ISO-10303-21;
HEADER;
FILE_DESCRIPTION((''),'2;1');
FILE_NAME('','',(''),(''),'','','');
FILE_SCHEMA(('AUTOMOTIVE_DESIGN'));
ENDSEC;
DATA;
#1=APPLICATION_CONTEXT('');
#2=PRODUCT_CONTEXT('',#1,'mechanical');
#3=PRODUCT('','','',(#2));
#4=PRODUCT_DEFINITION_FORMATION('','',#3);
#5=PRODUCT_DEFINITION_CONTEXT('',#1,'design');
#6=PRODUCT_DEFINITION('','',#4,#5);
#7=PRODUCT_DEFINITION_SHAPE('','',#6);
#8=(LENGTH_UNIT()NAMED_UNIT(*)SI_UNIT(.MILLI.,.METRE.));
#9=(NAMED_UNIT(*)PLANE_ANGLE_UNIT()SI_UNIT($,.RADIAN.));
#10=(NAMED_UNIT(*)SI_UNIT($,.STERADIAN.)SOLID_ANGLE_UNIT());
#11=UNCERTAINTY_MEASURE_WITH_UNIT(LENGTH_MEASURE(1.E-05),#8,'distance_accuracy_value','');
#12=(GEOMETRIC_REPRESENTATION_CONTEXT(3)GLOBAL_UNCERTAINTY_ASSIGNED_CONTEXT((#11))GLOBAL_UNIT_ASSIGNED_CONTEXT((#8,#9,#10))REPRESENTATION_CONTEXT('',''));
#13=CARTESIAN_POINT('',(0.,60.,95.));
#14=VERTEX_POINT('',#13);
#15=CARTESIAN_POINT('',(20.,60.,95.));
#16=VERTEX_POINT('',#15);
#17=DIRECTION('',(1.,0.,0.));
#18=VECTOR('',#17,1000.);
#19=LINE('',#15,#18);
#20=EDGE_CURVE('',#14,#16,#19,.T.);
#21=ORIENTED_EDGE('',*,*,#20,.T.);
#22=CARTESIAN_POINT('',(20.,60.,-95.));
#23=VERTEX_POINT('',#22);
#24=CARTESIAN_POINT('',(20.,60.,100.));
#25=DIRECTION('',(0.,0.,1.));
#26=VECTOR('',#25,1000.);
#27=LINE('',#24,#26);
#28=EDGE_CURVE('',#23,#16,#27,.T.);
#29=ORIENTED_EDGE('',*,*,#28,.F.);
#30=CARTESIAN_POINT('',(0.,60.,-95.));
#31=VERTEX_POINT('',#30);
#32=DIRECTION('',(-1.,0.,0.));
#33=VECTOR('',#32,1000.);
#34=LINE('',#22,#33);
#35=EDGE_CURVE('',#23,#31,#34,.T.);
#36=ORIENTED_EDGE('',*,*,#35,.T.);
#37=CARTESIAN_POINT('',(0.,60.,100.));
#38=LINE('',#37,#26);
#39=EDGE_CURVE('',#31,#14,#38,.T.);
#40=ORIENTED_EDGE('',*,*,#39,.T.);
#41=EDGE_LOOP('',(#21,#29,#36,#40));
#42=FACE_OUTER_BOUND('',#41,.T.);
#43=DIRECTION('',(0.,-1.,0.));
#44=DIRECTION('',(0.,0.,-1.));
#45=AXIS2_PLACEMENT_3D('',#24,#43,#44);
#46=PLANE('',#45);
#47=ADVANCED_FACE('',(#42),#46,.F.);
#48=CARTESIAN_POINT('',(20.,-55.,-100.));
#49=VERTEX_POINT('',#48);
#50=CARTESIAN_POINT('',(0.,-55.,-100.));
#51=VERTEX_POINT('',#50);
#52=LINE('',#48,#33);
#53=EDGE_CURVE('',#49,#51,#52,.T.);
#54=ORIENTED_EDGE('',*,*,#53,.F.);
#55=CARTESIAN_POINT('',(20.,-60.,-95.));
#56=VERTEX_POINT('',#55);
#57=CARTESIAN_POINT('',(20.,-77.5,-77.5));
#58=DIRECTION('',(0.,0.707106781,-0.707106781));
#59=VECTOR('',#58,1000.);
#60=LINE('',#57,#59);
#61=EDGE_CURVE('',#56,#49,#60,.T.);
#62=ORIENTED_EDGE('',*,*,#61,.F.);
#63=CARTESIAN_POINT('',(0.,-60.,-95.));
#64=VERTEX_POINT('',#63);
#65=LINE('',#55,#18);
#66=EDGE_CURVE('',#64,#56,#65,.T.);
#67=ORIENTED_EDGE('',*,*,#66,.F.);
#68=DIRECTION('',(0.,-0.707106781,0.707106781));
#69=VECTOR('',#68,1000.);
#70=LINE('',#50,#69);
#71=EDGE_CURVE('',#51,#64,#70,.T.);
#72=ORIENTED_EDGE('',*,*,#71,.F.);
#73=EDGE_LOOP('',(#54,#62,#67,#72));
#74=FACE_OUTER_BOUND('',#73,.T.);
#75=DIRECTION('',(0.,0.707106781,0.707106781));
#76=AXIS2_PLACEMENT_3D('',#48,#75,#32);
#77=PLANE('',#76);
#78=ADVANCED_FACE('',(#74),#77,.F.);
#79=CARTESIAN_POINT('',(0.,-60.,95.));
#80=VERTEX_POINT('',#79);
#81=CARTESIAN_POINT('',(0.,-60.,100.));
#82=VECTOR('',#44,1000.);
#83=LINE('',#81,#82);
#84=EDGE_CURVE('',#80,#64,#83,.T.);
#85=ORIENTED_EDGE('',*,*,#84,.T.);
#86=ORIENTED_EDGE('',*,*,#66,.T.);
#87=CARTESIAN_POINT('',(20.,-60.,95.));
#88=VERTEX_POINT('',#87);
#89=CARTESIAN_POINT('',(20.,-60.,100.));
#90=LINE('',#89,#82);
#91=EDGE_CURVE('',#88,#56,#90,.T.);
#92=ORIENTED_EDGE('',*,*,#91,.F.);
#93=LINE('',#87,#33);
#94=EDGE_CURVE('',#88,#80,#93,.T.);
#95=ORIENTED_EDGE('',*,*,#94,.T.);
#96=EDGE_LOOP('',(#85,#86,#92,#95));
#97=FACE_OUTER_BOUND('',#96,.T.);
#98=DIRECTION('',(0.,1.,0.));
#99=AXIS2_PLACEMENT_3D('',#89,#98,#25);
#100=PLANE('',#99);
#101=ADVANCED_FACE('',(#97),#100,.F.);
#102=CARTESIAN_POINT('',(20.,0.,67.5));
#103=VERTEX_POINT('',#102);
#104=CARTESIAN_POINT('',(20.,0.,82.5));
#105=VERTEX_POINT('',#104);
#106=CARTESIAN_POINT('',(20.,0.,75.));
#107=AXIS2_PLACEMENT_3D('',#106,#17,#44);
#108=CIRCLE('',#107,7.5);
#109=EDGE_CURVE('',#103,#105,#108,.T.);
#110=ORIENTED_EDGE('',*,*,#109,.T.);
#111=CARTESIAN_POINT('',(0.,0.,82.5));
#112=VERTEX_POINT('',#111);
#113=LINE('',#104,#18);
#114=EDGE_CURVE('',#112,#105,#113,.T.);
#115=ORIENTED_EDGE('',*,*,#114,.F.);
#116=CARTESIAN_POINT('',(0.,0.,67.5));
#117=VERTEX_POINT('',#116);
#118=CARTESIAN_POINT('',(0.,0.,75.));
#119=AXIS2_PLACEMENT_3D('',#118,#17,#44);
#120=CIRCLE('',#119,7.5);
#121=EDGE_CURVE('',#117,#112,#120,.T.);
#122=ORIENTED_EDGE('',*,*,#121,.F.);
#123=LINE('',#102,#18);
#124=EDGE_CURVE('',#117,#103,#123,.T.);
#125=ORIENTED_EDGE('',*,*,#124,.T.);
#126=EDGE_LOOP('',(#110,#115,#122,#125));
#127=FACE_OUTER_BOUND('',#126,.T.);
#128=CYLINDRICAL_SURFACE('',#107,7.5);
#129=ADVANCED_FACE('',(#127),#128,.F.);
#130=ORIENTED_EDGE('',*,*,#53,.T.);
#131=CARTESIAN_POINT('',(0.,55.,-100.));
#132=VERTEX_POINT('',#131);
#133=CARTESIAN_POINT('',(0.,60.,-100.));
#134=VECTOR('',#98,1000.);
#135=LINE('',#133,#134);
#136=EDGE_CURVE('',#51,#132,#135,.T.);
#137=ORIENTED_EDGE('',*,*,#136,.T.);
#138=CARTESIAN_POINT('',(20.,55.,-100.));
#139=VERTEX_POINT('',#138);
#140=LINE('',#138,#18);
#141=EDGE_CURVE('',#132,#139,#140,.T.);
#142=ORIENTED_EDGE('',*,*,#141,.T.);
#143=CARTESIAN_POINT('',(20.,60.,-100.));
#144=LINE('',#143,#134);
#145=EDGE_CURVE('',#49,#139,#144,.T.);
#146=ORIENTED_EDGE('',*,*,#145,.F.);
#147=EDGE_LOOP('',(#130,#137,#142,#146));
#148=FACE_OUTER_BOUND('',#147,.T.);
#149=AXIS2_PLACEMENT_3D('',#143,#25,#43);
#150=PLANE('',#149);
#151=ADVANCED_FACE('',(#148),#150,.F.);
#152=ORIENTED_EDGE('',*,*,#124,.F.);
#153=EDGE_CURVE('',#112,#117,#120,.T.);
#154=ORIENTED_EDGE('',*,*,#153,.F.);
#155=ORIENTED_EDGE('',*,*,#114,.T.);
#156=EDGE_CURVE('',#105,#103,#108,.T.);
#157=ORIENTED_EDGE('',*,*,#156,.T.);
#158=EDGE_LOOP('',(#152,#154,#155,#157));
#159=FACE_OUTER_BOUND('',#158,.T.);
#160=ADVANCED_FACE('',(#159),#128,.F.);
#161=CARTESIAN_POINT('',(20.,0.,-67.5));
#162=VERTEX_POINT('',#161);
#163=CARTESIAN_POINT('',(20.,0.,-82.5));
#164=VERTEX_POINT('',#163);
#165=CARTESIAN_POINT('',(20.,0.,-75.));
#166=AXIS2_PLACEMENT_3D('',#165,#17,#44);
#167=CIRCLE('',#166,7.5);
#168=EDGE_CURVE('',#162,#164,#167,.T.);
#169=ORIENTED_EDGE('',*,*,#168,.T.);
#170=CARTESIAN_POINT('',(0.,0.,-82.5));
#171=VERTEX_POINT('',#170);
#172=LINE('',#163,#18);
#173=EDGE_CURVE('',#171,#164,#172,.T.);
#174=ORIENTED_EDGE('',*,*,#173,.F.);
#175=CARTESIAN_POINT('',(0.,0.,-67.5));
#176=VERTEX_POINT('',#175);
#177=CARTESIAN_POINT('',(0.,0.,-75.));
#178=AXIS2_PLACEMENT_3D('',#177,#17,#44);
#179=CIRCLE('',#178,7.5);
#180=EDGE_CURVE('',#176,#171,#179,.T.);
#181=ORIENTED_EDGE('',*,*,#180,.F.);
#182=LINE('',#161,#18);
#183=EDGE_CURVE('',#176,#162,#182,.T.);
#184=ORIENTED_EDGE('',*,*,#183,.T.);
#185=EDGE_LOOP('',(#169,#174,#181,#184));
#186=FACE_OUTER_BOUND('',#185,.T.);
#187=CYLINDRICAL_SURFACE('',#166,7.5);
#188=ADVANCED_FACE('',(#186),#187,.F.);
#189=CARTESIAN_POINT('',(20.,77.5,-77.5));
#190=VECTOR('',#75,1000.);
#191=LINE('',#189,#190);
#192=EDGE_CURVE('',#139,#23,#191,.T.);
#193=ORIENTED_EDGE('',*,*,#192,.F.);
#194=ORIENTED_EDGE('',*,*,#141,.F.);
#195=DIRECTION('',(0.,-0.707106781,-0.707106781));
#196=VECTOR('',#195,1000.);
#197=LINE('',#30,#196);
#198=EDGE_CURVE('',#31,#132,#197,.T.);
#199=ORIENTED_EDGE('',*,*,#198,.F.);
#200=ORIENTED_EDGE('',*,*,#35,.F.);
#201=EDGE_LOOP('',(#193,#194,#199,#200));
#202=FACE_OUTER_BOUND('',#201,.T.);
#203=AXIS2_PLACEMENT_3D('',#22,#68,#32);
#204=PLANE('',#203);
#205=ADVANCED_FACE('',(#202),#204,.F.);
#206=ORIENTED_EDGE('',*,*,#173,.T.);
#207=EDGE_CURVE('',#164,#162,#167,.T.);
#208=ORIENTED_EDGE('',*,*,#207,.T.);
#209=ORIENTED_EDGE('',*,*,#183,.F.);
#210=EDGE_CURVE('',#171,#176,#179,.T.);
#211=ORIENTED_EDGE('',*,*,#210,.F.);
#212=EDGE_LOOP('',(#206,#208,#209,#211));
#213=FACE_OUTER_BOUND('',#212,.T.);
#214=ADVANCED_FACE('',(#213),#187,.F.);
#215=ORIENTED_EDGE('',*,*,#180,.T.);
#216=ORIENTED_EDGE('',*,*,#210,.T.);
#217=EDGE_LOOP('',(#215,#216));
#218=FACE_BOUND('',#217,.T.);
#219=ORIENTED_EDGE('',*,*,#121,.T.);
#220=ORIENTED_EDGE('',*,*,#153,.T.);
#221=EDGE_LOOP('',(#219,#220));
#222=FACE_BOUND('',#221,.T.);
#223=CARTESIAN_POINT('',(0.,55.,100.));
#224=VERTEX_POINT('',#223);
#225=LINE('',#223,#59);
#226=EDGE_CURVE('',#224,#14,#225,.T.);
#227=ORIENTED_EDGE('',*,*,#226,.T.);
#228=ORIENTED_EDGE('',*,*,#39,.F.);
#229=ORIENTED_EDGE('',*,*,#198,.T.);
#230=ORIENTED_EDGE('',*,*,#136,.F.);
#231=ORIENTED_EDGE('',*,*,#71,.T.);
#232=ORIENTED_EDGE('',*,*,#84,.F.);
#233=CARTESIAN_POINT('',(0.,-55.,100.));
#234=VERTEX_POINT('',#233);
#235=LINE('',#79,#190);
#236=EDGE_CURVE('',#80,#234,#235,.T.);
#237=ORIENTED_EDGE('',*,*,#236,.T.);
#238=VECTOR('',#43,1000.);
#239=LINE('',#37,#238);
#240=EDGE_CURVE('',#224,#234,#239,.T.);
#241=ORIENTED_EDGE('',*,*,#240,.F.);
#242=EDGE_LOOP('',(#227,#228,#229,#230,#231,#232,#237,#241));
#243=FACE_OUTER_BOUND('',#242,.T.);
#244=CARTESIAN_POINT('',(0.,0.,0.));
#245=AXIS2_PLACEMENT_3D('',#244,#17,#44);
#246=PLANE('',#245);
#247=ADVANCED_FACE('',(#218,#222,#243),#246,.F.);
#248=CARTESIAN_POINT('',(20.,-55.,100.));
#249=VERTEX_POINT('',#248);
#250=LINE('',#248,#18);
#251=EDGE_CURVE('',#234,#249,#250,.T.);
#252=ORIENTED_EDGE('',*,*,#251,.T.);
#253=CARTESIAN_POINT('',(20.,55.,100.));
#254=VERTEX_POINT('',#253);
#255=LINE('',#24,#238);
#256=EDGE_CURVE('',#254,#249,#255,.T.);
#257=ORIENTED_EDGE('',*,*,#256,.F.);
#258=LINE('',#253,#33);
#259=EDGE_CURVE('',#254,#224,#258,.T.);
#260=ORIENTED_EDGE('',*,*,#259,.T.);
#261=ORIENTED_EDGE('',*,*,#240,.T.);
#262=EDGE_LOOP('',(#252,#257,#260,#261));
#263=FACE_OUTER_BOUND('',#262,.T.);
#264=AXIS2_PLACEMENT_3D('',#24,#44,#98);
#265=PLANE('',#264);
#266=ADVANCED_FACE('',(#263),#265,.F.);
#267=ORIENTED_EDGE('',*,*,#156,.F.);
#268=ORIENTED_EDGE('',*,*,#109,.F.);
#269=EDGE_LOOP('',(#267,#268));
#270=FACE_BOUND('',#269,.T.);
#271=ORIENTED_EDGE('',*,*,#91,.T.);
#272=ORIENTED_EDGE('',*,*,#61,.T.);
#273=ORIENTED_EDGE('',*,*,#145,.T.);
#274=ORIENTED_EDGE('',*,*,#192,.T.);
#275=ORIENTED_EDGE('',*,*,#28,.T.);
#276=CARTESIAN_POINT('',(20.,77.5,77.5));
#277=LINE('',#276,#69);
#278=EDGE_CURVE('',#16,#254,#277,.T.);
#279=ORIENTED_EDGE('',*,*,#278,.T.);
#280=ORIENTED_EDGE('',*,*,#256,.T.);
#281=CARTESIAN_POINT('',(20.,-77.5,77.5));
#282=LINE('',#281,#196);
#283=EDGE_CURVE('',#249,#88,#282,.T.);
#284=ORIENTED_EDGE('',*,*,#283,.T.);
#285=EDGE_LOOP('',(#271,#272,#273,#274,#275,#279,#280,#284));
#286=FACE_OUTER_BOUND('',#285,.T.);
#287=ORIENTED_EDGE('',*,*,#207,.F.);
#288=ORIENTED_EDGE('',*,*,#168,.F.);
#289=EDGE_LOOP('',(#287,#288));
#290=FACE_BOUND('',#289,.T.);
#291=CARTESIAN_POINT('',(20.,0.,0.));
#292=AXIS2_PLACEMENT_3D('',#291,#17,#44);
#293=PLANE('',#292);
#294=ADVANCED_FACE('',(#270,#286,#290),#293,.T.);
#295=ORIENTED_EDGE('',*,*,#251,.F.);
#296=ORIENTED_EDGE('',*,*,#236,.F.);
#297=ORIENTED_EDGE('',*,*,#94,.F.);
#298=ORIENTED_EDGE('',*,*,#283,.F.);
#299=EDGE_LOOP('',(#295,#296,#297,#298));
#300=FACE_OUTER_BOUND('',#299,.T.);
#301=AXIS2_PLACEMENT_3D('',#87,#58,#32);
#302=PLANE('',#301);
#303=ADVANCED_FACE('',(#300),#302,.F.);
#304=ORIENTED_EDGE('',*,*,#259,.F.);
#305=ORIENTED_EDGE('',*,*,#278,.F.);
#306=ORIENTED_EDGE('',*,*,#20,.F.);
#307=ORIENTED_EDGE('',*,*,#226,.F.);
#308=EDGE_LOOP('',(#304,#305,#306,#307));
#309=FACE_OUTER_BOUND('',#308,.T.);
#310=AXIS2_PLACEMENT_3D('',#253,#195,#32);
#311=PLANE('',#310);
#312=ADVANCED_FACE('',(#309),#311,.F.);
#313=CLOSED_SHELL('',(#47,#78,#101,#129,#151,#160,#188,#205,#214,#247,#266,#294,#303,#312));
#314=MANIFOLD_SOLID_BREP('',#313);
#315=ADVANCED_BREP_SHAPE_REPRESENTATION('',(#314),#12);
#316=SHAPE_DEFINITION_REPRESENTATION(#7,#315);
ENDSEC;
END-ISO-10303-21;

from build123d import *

# Parameters (mm, degrees)
SKETCH_1_W              = 200
SKETCH_1_H              = 120
EXTRUDE_1_DEPTH         = 20
HOLE_WIZARD_15_0_15_1_D = 15
CHAMFER_1_SIZE          = 5


with BuildPart() as part:
    # 草图1 → 凸台-拉伸1 (new body)
    with BuildSketch(Plane(origin=(0, 0, 0), x_dir=(0, 0, -1), z_dir=(1, 0, 0))):
        Rectangle(SKETCH_1_W, SKETCH_1_H)
    extrude(amount=EXTRUDE_1_DEPTH)

    # Ø15.0 (15) 直径孔1 (through all)
    with Locations(Plane(origin=(20, 0, 0), x_dir=(0, 0, -1), z_dir=(1, 0, 0))):
        with Locations((-75, 0), (75, 0)):
            Hole(HOLE_WIZARD_15_0_15_1_D / 2)

    # 倒角1
    chamfer_1_edges = [part.edges().sort_by_distance(p)[0] for p in [
        (10, -60, -100),
        (10, -60, 100),
        (10, 60, 100),
        (10, 60, -100),
    ]]
    chamfer(chamfer_1_edges, length=CHAMFER_1_SIZE)


solid = part.part
